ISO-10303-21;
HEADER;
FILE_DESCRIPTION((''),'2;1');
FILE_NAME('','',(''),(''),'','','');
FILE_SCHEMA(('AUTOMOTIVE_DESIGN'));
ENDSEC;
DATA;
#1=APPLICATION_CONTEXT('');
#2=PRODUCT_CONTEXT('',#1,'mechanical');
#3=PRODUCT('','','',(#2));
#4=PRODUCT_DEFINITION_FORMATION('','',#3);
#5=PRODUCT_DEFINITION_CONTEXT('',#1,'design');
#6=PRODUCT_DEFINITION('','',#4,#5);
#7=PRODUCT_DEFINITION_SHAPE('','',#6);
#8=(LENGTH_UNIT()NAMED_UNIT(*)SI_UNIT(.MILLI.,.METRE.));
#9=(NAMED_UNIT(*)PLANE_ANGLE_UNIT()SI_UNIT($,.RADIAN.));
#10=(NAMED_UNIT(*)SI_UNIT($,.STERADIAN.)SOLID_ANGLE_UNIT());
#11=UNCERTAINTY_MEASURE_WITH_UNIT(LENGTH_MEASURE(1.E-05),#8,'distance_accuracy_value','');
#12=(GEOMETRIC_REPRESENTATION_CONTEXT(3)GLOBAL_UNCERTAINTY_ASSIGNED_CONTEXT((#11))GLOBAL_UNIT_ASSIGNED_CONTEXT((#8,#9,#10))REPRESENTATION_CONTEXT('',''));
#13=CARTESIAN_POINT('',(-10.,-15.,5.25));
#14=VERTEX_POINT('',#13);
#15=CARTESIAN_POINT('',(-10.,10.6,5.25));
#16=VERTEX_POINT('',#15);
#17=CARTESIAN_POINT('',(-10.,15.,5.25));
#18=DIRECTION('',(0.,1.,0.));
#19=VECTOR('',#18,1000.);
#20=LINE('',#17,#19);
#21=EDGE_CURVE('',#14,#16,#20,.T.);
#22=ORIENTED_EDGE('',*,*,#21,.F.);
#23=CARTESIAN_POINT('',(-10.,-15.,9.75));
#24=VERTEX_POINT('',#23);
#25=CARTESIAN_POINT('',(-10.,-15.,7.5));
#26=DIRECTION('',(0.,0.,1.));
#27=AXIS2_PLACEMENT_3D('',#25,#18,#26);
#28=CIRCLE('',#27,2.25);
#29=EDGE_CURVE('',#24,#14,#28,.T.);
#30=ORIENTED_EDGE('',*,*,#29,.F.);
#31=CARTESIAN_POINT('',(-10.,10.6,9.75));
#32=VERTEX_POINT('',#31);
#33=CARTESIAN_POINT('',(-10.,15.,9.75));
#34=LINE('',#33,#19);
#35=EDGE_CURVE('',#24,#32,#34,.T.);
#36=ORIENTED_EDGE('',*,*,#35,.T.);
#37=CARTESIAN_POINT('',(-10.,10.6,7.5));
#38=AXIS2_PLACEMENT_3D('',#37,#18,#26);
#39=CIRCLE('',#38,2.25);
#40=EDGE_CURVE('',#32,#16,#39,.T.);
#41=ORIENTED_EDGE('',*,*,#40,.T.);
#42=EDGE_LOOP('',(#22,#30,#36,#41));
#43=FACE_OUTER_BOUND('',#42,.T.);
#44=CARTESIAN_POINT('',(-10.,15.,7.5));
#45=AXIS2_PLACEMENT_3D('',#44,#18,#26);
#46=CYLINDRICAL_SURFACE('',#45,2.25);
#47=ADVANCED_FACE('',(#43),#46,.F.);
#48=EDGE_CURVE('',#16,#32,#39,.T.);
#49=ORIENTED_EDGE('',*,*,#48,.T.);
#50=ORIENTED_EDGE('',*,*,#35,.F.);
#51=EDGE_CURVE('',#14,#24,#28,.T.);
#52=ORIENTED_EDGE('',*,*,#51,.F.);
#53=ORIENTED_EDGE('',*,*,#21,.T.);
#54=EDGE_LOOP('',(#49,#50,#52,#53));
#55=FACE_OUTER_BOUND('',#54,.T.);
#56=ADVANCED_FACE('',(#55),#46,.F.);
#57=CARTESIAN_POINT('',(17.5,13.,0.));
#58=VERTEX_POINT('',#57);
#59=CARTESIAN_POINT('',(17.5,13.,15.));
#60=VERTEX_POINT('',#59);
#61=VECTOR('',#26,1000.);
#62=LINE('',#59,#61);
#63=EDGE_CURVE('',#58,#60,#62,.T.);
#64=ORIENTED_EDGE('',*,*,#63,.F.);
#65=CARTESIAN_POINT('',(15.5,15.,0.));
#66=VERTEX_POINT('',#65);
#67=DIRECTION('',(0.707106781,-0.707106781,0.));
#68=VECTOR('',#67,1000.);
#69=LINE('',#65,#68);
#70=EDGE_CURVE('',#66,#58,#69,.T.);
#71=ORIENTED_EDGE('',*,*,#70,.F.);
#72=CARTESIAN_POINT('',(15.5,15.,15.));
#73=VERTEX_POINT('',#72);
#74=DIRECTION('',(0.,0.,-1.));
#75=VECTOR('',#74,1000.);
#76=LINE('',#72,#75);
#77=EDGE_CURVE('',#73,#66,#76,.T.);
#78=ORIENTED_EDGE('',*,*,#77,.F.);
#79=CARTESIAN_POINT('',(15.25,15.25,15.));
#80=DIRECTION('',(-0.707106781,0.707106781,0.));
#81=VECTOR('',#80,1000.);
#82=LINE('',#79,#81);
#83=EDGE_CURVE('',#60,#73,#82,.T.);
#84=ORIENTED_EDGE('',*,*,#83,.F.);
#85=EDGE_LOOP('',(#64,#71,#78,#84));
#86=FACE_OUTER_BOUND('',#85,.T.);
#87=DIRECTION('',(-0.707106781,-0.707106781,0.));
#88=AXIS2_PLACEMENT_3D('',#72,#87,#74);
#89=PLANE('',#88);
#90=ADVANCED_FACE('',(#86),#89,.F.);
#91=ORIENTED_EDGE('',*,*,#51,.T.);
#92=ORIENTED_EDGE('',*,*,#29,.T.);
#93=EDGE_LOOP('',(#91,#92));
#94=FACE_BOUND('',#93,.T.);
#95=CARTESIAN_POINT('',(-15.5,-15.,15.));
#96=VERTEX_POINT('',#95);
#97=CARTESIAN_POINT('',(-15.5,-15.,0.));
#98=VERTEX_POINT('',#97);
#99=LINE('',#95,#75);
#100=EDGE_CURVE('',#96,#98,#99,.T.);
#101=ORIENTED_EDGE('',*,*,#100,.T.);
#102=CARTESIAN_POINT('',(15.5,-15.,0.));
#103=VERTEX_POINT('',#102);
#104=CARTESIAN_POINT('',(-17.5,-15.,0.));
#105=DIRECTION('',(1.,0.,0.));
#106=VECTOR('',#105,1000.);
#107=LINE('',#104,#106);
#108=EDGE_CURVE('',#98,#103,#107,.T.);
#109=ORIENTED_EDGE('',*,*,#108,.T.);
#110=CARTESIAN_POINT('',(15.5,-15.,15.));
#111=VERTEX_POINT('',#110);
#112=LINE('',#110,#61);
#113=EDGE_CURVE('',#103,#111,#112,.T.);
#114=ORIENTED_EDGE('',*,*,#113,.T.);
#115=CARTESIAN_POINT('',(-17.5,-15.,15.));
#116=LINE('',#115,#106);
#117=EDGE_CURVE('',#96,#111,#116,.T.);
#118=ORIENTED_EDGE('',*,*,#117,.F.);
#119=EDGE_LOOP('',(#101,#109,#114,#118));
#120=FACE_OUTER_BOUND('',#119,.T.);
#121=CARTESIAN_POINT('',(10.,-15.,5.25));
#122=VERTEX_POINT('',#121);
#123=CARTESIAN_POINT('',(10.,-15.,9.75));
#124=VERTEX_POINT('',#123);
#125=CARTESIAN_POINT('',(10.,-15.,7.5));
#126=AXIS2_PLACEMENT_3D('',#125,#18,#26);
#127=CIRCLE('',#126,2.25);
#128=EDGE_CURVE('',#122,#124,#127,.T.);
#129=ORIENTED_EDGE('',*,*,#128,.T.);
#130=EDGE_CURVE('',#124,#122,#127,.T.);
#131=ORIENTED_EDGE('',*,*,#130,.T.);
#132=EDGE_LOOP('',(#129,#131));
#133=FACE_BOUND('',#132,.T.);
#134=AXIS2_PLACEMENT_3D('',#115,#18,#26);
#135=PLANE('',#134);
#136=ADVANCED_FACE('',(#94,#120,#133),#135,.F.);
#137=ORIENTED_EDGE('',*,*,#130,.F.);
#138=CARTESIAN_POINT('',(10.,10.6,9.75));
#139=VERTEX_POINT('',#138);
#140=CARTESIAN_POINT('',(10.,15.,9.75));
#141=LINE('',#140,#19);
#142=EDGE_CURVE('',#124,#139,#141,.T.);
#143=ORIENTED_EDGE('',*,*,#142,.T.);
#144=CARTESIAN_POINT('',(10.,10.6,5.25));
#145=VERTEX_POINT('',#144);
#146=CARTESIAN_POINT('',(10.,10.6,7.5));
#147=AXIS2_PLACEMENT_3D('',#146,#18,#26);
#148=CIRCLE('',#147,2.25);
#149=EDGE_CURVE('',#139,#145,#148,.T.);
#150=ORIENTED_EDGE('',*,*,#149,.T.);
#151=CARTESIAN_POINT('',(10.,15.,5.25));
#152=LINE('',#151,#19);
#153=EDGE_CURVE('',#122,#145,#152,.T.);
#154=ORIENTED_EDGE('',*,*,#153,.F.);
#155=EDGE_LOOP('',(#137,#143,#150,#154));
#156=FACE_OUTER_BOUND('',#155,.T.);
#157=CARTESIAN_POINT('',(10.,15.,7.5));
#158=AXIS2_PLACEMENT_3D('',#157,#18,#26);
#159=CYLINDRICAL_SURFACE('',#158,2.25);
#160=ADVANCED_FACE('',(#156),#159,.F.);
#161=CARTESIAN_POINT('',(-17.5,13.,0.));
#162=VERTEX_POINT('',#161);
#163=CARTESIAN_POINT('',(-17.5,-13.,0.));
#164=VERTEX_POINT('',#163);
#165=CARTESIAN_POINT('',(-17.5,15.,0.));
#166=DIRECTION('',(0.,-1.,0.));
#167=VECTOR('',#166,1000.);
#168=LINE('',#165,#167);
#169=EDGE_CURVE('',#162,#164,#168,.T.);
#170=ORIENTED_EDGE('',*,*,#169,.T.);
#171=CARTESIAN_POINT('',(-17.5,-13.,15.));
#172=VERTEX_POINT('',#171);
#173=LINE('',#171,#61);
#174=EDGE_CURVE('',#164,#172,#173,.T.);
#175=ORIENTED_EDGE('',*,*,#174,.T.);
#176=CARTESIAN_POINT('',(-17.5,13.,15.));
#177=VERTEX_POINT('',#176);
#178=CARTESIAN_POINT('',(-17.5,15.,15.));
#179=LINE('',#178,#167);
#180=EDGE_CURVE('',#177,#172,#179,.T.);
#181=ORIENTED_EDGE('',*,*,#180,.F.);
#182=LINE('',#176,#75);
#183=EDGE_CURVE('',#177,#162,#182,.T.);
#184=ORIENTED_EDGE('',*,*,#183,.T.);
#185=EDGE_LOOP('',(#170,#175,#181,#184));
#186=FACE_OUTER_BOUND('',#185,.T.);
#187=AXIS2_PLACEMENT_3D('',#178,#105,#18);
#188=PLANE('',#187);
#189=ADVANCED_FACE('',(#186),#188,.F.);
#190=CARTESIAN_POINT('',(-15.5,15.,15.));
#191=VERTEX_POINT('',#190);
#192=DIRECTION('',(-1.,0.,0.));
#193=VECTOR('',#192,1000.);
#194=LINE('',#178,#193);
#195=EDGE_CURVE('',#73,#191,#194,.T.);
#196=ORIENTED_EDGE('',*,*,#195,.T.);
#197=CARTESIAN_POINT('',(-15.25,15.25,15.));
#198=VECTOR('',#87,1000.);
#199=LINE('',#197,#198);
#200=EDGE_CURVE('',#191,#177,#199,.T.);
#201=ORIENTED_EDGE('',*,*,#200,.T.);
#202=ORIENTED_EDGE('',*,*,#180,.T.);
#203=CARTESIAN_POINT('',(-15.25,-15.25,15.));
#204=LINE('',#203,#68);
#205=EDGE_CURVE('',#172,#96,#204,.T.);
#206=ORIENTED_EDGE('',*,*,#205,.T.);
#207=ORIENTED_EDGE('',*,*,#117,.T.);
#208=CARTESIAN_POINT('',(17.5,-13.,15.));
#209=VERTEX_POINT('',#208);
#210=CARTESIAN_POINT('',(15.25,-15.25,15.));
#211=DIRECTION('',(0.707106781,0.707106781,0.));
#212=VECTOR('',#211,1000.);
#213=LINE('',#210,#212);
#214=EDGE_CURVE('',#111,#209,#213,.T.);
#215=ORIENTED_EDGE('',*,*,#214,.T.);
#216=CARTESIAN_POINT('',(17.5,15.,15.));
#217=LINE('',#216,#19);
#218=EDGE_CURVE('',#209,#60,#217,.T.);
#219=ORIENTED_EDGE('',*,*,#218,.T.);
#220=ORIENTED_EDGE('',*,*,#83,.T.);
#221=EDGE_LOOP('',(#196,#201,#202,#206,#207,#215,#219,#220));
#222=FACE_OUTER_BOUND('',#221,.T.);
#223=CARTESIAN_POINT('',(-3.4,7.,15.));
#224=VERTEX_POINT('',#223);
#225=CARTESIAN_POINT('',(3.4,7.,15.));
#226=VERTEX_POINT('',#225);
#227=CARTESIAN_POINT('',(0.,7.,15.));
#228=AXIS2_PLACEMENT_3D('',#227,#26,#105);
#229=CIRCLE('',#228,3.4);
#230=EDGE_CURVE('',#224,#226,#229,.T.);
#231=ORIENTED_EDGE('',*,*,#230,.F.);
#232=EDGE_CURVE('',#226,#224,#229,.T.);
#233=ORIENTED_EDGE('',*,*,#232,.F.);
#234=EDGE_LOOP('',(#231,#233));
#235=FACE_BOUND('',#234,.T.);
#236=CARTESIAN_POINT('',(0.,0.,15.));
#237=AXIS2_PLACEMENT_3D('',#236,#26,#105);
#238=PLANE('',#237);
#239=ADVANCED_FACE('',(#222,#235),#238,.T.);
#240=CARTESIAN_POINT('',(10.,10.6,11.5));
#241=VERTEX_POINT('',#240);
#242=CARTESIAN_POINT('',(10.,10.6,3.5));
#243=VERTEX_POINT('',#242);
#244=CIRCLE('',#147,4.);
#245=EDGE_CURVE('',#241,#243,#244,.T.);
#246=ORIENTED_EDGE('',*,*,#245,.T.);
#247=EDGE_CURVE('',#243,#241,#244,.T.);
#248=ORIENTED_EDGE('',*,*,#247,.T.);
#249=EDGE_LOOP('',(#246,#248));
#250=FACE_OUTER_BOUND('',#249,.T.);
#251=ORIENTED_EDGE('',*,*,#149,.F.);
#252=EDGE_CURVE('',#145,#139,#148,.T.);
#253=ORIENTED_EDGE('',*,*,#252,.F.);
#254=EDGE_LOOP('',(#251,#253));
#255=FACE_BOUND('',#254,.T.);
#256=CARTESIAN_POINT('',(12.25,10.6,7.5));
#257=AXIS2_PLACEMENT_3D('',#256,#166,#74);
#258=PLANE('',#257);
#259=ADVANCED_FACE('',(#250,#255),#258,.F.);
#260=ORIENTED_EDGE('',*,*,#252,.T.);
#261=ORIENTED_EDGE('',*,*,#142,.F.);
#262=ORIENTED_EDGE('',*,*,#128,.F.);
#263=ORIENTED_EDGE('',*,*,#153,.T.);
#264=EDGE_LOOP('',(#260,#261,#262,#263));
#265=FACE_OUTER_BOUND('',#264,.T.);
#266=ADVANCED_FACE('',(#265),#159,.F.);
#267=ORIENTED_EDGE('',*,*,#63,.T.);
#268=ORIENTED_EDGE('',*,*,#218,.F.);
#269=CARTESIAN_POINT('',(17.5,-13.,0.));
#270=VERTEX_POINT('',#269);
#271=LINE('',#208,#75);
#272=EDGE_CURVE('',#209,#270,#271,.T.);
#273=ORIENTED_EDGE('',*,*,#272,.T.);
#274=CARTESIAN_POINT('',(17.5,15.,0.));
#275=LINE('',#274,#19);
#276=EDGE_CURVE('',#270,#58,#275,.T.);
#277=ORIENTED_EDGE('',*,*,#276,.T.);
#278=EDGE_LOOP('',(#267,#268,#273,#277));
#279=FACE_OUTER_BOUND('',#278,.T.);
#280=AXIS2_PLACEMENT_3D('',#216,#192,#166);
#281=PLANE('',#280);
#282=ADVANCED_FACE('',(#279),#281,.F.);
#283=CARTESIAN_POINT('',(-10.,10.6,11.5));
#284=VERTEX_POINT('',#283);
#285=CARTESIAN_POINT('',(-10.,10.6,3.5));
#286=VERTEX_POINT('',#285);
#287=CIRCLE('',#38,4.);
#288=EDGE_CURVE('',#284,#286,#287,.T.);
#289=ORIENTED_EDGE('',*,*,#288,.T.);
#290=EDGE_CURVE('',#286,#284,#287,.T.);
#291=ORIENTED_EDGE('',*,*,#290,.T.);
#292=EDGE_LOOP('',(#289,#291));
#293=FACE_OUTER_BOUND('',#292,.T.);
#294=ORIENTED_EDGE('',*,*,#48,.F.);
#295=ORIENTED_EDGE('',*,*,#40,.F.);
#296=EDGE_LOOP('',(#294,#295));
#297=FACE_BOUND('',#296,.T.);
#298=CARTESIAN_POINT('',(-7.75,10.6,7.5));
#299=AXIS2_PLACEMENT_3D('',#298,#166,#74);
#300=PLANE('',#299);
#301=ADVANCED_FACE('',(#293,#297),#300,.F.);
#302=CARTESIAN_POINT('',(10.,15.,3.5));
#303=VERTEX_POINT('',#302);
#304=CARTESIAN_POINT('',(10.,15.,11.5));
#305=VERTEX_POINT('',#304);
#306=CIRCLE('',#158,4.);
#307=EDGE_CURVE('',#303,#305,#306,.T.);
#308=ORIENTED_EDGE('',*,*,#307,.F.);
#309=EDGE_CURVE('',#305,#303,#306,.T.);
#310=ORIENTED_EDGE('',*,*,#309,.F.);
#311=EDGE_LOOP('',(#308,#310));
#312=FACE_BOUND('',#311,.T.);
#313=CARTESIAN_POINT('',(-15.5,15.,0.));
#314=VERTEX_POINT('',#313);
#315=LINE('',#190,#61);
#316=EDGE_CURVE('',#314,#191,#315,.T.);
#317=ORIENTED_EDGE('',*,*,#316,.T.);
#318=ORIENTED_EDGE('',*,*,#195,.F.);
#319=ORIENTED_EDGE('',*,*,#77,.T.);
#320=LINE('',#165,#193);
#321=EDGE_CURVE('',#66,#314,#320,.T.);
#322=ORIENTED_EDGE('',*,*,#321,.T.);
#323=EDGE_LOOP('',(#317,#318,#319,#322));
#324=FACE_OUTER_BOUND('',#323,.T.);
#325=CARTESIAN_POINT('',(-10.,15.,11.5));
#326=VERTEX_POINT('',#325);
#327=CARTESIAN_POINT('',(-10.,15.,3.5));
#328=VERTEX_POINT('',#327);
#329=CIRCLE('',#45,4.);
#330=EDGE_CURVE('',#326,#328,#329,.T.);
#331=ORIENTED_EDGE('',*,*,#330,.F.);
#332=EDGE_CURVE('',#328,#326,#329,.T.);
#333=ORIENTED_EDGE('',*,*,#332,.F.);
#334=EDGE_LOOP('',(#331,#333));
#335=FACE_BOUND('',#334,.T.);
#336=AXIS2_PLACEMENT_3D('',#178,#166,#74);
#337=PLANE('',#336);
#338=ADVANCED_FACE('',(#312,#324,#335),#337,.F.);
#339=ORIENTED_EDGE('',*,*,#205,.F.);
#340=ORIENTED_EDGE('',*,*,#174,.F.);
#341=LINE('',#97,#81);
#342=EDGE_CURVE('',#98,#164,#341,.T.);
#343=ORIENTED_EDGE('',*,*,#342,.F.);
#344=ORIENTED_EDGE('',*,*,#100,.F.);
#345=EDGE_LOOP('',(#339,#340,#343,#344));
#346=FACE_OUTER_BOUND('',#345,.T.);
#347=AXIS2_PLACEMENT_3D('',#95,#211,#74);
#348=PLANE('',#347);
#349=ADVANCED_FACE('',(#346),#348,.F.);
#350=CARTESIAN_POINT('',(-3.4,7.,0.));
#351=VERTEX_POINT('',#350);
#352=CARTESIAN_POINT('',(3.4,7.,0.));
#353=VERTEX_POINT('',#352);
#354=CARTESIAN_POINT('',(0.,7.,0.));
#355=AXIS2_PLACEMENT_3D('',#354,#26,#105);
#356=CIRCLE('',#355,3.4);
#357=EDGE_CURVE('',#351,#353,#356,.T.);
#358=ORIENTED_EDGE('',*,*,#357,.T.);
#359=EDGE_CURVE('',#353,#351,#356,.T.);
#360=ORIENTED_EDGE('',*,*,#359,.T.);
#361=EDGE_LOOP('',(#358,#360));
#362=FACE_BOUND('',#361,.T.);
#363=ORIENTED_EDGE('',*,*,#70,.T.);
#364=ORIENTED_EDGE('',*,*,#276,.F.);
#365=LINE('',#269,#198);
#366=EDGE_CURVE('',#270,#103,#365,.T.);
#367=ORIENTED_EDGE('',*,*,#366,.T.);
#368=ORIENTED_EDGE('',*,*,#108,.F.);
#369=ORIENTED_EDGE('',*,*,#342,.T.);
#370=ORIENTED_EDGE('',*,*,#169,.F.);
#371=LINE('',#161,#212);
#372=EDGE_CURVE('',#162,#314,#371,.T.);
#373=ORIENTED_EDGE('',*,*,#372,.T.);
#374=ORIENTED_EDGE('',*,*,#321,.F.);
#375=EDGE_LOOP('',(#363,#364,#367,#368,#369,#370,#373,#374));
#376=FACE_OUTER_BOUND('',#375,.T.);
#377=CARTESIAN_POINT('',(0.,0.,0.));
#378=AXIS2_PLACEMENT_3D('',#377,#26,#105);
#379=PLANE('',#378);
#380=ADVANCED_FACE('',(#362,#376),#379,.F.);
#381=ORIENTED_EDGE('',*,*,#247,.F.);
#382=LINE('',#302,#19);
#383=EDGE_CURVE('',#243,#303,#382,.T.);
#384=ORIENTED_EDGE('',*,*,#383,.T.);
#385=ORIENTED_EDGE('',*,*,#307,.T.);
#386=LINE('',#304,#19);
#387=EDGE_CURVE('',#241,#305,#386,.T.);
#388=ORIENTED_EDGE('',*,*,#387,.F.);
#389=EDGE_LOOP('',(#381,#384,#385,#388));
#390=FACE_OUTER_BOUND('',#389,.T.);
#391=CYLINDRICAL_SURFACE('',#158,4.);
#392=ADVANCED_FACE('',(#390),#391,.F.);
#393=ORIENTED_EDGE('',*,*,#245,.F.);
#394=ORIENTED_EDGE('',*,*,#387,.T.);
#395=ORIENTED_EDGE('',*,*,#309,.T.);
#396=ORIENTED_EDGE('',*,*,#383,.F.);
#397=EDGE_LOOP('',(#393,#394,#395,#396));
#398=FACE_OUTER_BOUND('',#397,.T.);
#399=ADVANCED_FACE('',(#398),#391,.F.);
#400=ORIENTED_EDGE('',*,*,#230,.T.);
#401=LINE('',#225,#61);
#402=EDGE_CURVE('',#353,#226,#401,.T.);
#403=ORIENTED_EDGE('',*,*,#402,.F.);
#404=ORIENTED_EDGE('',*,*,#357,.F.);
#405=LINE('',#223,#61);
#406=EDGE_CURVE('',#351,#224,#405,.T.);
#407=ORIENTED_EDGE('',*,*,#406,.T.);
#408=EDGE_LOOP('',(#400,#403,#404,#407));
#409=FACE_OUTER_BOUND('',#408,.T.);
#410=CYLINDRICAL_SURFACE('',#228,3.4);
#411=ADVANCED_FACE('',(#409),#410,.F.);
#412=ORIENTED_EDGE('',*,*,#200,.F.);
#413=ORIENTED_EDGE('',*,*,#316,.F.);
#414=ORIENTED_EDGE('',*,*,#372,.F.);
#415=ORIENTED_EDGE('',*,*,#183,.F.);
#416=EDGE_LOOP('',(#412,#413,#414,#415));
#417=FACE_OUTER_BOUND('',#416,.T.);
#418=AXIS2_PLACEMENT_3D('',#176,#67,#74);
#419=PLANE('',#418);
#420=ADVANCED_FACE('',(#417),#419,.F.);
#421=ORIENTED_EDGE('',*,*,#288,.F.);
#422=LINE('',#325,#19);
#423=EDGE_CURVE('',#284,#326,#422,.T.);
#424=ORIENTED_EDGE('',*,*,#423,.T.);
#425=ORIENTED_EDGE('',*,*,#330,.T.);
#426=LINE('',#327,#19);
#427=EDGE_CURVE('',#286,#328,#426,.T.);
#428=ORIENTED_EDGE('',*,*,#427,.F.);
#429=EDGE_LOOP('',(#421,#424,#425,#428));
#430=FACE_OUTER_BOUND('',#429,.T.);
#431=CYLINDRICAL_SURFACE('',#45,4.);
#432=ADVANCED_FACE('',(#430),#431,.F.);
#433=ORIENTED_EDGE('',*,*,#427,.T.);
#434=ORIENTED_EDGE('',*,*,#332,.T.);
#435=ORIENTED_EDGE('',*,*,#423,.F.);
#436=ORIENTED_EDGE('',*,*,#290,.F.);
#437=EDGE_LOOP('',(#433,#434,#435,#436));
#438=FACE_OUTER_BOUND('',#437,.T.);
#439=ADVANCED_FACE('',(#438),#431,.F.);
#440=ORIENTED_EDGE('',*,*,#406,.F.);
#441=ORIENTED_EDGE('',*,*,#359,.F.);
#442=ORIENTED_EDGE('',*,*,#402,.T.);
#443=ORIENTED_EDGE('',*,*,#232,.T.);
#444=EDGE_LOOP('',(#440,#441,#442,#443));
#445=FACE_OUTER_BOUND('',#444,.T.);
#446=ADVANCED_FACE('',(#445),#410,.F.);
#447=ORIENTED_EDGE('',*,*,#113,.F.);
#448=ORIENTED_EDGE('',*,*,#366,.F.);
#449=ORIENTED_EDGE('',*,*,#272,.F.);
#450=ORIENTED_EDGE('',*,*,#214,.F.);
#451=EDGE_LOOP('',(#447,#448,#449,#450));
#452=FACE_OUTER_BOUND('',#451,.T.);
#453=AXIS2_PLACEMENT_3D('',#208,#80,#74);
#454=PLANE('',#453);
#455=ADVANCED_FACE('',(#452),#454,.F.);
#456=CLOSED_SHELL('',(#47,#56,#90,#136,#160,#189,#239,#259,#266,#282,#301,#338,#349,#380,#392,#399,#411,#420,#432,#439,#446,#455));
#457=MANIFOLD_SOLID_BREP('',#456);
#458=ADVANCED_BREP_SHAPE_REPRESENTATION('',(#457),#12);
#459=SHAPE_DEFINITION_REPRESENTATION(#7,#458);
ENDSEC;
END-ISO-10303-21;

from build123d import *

# Parameters (mm, degrees)
SKETCH1_W                                           = 35
SKETCH1_H                                           = 30
BOSS_EXTRUDE1_DEPTH                                 = 15
CBORE_FOR_M4_HEX_SOCKET_HEAD_CAP_SCREW1_D           = 4.5
CBORE_FOR_M4_HEX_SOCKET_HEAD_CAP_SCREW1_CBORE_D     = 8
CBORE_FOR_M4_HEX_SOCKET_HEAD_CAP_SCREW1_CBORE_DEPTH = 4.4
M8_TAPPED_HOLE1_D                                   = 6.8
M8_TAPPED_HOLE1_DEPTH                               = 22.25
M8_TAPPED_HOLE1_TIP                                 = 2.042926105
CHAMFER1_SIZE                                       = 2


with BuildPart() as part:
    # Sketch1 → Boss-Extrude1 (new body)
    with BuildSketch(Plane.XY):
        Rectangle(SKETCH1_W, SKETCH1_H)
    extrude(amount=BOSS_EXTRUDE1_DEPTH)

    # CBORE for M4 Hex Socket Head Cap Screw1 (through all)
    with Locations(Plane(origin=(0, 15, 0), x_dir=(1, 0, 0), z_dir=(0, 1, 0))):
        with Locations((-10, -7.5), (10, -7.5)):
            CounterBoreHole(CBORE_FOR_M4_HEX_SOCKET_HEAD_CAP_SCREW1_D / 2, CBORE_FOR_M4_HEX_SOCKET_HEAD_CAP_SCREW1_CBORE_D / 2, CBORE_FOR_M4_HEX_SOCKET_HEAD_CAP_SCREW1_CBORE_DEPTH)

    # M8 Tapped Hole1
    with Locations(Plane.XY.offset(15)):
        with Locations((0, 7)):
            Hole(M8_TAPPED_HOLE1_D / 2, depth=M8_TAPPED_HOLE1_DEPTH)
            with Locations((0, 0, -(M8_TAPPED_HOLE1_DEPTH + M8_TAPPED_HOLE1_TIP / 2))):  # 118° drill point
                Cone(0, M8_TAPPED_HOLE1_D / 2, M8_TAPPED_HOLE1_TIP, mode=Mode.SUBTRACT)

    # Chamfer1
    chamfer1_edges = [part.edges().sort_by_distance(p)[0] for p in [
        (17.5, -15, 7.5),
        (-17.5, -15, 7.5),
        (-17.5, 15, 7.5),
        (17.5, 15, 7.5),
    ]]
    chamfer(chamfer1_edges, length=CHAMFER1_SIZE)


solid = part.part
